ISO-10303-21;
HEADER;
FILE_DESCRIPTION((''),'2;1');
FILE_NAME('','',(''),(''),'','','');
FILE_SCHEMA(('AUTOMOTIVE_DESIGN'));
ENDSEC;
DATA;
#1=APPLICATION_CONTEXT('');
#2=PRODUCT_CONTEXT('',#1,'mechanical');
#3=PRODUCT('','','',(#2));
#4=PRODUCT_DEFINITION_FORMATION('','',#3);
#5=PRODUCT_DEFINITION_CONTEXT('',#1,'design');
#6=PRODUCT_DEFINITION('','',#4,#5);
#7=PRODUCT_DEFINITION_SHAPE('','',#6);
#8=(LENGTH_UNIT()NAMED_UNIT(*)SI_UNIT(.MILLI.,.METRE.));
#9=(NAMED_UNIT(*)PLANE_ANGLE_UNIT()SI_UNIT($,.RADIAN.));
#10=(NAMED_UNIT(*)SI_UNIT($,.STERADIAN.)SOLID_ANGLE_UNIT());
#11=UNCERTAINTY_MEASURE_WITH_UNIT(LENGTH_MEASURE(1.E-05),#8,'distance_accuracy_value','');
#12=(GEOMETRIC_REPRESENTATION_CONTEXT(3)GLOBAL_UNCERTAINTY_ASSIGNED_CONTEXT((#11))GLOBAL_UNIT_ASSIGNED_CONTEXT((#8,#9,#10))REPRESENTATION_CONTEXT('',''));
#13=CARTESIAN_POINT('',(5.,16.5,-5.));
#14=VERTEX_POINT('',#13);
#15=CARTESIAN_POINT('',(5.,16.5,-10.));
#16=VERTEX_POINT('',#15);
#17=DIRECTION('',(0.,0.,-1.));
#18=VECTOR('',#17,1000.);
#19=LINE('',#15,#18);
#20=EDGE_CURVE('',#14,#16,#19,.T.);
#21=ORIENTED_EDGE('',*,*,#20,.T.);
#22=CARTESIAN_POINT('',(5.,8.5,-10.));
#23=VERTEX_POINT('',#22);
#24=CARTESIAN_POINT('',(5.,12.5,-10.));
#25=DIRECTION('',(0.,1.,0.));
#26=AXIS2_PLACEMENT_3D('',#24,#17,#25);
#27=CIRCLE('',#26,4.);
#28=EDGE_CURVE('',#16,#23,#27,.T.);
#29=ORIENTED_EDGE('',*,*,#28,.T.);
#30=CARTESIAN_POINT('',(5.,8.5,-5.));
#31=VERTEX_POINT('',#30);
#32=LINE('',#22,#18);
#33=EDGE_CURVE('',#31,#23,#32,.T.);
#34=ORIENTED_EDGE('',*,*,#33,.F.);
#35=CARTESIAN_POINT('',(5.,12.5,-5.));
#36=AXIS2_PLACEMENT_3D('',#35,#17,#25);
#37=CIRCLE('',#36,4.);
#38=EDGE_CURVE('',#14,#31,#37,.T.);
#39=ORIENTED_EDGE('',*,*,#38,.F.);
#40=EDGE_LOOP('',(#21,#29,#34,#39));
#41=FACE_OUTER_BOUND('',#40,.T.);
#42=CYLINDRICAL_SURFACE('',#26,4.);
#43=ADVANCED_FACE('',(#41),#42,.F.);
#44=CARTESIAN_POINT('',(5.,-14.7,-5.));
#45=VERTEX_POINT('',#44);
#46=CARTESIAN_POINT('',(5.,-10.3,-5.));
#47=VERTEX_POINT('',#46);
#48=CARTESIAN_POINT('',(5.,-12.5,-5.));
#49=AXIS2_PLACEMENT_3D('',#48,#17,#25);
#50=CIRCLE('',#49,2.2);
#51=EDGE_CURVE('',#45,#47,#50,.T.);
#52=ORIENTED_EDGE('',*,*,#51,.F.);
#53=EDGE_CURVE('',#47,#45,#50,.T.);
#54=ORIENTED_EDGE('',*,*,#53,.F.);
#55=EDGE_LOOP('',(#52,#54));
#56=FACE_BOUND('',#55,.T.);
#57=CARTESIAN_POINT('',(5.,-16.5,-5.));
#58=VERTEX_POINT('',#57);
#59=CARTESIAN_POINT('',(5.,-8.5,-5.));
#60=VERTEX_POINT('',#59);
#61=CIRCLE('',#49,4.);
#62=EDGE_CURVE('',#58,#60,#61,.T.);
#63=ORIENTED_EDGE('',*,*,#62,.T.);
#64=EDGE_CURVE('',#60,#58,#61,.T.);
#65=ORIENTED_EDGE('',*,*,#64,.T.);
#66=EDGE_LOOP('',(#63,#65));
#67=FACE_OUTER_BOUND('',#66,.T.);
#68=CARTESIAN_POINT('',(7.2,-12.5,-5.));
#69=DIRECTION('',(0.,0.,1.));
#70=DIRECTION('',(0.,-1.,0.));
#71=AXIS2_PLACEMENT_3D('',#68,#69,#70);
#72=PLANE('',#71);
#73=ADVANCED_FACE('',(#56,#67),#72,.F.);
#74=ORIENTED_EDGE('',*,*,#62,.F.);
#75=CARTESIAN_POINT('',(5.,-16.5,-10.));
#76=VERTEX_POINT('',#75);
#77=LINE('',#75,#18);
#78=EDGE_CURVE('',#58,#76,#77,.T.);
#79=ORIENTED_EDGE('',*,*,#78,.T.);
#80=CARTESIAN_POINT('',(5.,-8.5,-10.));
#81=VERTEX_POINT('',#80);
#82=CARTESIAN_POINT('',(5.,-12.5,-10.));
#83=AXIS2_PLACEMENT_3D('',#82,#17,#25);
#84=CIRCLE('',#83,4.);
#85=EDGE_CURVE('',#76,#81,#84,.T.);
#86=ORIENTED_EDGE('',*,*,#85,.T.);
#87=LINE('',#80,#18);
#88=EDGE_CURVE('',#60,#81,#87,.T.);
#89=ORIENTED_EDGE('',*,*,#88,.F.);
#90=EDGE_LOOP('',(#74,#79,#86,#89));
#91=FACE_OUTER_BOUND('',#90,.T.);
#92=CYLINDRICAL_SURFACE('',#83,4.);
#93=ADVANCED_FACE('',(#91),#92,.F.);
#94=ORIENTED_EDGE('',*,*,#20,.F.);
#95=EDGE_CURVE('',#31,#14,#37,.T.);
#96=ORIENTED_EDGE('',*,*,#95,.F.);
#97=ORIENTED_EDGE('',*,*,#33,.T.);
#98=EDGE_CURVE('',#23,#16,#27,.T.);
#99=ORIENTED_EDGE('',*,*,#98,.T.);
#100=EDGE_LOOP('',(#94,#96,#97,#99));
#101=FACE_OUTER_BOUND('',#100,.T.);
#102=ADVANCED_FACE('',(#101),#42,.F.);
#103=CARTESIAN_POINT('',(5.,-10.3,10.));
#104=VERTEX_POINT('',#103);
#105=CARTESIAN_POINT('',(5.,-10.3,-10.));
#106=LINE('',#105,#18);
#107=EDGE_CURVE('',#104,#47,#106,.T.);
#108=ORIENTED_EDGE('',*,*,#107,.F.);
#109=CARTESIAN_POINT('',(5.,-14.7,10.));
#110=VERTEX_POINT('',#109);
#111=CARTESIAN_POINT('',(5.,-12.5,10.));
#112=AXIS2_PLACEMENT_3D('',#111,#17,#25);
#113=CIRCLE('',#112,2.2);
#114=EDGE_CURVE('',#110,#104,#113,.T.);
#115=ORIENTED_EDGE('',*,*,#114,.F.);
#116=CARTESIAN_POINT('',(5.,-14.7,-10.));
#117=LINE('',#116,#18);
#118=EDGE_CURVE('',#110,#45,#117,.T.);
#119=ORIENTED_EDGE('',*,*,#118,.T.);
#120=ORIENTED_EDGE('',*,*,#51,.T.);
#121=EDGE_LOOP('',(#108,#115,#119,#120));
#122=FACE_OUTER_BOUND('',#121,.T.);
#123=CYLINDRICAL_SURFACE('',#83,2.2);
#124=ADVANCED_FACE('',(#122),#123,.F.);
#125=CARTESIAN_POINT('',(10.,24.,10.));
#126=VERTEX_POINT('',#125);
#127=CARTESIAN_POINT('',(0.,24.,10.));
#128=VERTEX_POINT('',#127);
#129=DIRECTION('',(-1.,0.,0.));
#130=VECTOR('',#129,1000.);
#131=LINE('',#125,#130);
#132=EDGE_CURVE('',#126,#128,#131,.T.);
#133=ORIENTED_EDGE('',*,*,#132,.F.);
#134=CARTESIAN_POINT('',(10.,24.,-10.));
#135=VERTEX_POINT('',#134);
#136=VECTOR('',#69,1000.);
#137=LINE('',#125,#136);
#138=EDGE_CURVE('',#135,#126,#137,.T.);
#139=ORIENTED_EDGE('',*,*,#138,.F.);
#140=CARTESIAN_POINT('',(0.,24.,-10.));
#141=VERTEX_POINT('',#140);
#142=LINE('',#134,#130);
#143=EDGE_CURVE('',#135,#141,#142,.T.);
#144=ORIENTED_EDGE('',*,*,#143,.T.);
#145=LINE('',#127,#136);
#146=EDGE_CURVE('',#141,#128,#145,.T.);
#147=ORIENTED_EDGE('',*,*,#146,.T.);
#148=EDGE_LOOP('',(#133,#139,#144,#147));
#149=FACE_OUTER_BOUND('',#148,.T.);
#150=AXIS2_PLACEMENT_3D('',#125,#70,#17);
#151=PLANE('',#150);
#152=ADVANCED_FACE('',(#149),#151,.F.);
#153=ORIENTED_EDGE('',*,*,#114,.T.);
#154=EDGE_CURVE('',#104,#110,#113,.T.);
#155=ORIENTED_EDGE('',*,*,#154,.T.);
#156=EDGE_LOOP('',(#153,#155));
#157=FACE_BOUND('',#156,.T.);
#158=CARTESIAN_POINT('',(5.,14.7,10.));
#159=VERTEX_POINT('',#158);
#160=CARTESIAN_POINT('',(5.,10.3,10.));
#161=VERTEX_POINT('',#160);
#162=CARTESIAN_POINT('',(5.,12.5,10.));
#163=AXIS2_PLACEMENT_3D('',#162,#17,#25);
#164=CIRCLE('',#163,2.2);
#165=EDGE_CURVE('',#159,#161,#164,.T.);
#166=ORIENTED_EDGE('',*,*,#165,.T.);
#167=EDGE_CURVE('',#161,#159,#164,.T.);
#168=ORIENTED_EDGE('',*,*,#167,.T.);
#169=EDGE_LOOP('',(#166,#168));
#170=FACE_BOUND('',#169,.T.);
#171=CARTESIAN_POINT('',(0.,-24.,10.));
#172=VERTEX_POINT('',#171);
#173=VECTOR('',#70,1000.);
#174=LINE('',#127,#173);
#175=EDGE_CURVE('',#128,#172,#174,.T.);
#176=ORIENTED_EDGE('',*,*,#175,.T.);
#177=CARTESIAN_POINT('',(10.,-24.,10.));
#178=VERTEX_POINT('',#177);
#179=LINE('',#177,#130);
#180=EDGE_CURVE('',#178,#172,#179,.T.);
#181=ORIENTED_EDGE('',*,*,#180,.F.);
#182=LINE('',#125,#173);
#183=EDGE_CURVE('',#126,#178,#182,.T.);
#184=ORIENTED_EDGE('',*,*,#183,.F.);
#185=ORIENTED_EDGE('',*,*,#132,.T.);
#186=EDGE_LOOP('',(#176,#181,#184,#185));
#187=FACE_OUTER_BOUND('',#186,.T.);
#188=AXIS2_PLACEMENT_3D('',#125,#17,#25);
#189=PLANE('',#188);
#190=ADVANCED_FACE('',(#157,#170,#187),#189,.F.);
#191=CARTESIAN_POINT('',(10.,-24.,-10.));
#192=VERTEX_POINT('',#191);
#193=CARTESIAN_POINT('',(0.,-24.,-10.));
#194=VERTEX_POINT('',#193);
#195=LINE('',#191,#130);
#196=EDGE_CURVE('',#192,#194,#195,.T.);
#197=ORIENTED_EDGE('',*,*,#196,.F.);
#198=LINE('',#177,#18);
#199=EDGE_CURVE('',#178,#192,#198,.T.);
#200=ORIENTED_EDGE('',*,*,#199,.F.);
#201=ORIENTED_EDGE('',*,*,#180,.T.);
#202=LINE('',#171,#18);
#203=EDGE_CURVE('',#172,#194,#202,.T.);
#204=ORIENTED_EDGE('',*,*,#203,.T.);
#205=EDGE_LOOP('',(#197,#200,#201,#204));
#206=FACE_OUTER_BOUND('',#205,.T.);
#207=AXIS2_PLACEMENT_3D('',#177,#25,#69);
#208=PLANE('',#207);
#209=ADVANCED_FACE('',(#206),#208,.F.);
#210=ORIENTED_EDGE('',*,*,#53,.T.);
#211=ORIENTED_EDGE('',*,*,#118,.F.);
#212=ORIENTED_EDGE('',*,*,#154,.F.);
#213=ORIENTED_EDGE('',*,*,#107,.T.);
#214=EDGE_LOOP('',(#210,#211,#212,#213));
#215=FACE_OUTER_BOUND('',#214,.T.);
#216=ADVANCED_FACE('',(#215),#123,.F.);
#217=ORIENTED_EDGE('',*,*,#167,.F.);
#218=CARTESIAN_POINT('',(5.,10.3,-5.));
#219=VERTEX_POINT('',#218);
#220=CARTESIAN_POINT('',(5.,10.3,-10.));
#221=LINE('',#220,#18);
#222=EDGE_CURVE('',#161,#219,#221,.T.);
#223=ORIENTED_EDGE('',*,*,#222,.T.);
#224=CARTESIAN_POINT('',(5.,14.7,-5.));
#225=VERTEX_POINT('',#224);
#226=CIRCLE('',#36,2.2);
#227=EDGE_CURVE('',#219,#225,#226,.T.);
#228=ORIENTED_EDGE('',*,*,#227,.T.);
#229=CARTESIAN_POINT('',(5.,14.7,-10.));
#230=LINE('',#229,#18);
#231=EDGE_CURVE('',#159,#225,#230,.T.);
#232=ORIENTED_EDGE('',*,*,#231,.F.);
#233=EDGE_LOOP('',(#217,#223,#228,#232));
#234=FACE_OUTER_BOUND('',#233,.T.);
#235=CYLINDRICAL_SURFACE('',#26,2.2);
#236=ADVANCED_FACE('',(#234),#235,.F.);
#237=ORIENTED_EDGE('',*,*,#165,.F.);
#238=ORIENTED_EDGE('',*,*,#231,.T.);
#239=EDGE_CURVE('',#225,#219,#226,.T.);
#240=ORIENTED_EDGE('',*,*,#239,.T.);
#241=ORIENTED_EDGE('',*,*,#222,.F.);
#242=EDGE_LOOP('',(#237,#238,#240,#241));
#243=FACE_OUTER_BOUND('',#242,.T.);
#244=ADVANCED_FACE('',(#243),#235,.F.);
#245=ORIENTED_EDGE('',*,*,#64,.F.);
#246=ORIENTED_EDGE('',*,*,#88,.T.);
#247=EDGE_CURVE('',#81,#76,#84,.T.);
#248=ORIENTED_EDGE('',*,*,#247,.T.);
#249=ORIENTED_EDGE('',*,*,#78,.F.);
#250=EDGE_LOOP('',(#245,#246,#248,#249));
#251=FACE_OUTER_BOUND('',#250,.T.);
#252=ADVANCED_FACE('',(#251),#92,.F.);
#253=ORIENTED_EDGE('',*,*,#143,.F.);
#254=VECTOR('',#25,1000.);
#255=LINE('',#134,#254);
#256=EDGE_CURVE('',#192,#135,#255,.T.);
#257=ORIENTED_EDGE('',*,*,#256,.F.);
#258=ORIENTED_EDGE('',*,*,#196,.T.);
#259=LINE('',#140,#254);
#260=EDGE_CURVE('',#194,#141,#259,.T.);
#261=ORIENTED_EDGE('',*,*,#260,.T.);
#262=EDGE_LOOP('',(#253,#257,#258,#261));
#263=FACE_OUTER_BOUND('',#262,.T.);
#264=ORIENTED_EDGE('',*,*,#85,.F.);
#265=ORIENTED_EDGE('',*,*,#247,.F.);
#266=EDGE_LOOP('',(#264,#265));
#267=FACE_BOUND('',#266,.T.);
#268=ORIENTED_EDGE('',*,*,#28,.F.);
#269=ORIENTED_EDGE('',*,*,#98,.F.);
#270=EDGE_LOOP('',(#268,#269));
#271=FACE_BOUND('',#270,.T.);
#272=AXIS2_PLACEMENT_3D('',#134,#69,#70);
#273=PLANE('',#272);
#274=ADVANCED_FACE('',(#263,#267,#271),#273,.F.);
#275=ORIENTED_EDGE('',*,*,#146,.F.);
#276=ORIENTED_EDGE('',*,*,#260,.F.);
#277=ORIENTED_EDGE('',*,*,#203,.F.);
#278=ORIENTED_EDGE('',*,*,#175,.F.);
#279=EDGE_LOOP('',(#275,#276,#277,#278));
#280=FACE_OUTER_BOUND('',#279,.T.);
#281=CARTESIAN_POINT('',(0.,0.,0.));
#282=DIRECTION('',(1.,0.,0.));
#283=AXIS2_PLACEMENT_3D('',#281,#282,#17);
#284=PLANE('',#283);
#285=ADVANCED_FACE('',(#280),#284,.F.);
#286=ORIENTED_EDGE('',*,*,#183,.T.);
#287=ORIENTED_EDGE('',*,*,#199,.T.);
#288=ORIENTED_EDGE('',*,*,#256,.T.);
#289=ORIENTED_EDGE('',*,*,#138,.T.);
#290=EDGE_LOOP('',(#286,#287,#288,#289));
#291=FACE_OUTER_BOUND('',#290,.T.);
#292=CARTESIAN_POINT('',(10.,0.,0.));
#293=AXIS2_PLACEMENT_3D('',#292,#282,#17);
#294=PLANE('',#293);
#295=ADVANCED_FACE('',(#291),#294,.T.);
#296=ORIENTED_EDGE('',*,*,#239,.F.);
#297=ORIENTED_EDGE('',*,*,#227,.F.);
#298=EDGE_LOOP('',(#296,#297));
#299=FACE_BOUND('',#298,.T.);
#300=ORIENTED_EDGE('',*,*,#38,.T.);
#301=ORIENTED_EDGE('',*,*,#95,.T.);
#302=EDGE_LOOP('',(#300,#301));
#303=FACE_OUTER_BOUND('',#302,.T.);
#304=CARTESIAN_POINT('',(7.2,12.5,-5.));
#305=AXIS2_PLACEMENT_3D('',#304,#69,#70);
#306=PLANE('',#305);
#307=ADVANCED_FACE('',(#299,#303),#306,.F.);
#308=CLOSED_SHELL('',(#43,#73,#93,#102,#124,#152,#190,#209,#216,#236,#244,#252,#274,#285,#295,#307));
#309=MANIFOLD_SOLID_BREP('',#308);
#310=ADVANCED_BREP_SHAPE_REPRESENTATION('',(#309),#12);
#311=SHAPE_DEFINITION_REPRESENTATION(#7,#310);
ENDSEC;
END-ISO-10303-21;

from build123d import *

# Parameters (mm, degrees)
SKETCH_1_W                = 20
SKETCH_1_H                = 48
EXTRUDE_1_DEPTH           = 10
HOLE_WIZARD_1_D           = 4.4
HOLE_WIZARD_1_CBORE_D     = 8
HOLE_WIZARD_1_CBORE_DEPTH = 5


with BuildPart() as part:
    # 草图1 → 凸台-拉伸1 (new body)
    with BuildSketch(Plane(origin=(0, 0, 0), x_dir=(0, 0, -1), z_dir=(1, 0, 0))):
        Rectangle(SKETCH_1_W, SKETCH_1_H)
    extrude(amount=EXTRUDE_1_DEPTH)

    # 打孔尺寸(%根据)内六角圆柱头螺钉的类型1 (through all)
    with Locations(Plane(origin=(0, 0, -10), x_dir=(-1, 0, 0), z_dir=(0, 0, -1))):
        with Locations((-5, -12.5), (-5, 12.5)):
            CounterBoreHole(HOLE_WIZARD_1_D / 2, HOLE_WIZARD_1_CBORE_D / 2, HOLE_WIZARD_1_CBORE_DEPTH)


solid = part.part
